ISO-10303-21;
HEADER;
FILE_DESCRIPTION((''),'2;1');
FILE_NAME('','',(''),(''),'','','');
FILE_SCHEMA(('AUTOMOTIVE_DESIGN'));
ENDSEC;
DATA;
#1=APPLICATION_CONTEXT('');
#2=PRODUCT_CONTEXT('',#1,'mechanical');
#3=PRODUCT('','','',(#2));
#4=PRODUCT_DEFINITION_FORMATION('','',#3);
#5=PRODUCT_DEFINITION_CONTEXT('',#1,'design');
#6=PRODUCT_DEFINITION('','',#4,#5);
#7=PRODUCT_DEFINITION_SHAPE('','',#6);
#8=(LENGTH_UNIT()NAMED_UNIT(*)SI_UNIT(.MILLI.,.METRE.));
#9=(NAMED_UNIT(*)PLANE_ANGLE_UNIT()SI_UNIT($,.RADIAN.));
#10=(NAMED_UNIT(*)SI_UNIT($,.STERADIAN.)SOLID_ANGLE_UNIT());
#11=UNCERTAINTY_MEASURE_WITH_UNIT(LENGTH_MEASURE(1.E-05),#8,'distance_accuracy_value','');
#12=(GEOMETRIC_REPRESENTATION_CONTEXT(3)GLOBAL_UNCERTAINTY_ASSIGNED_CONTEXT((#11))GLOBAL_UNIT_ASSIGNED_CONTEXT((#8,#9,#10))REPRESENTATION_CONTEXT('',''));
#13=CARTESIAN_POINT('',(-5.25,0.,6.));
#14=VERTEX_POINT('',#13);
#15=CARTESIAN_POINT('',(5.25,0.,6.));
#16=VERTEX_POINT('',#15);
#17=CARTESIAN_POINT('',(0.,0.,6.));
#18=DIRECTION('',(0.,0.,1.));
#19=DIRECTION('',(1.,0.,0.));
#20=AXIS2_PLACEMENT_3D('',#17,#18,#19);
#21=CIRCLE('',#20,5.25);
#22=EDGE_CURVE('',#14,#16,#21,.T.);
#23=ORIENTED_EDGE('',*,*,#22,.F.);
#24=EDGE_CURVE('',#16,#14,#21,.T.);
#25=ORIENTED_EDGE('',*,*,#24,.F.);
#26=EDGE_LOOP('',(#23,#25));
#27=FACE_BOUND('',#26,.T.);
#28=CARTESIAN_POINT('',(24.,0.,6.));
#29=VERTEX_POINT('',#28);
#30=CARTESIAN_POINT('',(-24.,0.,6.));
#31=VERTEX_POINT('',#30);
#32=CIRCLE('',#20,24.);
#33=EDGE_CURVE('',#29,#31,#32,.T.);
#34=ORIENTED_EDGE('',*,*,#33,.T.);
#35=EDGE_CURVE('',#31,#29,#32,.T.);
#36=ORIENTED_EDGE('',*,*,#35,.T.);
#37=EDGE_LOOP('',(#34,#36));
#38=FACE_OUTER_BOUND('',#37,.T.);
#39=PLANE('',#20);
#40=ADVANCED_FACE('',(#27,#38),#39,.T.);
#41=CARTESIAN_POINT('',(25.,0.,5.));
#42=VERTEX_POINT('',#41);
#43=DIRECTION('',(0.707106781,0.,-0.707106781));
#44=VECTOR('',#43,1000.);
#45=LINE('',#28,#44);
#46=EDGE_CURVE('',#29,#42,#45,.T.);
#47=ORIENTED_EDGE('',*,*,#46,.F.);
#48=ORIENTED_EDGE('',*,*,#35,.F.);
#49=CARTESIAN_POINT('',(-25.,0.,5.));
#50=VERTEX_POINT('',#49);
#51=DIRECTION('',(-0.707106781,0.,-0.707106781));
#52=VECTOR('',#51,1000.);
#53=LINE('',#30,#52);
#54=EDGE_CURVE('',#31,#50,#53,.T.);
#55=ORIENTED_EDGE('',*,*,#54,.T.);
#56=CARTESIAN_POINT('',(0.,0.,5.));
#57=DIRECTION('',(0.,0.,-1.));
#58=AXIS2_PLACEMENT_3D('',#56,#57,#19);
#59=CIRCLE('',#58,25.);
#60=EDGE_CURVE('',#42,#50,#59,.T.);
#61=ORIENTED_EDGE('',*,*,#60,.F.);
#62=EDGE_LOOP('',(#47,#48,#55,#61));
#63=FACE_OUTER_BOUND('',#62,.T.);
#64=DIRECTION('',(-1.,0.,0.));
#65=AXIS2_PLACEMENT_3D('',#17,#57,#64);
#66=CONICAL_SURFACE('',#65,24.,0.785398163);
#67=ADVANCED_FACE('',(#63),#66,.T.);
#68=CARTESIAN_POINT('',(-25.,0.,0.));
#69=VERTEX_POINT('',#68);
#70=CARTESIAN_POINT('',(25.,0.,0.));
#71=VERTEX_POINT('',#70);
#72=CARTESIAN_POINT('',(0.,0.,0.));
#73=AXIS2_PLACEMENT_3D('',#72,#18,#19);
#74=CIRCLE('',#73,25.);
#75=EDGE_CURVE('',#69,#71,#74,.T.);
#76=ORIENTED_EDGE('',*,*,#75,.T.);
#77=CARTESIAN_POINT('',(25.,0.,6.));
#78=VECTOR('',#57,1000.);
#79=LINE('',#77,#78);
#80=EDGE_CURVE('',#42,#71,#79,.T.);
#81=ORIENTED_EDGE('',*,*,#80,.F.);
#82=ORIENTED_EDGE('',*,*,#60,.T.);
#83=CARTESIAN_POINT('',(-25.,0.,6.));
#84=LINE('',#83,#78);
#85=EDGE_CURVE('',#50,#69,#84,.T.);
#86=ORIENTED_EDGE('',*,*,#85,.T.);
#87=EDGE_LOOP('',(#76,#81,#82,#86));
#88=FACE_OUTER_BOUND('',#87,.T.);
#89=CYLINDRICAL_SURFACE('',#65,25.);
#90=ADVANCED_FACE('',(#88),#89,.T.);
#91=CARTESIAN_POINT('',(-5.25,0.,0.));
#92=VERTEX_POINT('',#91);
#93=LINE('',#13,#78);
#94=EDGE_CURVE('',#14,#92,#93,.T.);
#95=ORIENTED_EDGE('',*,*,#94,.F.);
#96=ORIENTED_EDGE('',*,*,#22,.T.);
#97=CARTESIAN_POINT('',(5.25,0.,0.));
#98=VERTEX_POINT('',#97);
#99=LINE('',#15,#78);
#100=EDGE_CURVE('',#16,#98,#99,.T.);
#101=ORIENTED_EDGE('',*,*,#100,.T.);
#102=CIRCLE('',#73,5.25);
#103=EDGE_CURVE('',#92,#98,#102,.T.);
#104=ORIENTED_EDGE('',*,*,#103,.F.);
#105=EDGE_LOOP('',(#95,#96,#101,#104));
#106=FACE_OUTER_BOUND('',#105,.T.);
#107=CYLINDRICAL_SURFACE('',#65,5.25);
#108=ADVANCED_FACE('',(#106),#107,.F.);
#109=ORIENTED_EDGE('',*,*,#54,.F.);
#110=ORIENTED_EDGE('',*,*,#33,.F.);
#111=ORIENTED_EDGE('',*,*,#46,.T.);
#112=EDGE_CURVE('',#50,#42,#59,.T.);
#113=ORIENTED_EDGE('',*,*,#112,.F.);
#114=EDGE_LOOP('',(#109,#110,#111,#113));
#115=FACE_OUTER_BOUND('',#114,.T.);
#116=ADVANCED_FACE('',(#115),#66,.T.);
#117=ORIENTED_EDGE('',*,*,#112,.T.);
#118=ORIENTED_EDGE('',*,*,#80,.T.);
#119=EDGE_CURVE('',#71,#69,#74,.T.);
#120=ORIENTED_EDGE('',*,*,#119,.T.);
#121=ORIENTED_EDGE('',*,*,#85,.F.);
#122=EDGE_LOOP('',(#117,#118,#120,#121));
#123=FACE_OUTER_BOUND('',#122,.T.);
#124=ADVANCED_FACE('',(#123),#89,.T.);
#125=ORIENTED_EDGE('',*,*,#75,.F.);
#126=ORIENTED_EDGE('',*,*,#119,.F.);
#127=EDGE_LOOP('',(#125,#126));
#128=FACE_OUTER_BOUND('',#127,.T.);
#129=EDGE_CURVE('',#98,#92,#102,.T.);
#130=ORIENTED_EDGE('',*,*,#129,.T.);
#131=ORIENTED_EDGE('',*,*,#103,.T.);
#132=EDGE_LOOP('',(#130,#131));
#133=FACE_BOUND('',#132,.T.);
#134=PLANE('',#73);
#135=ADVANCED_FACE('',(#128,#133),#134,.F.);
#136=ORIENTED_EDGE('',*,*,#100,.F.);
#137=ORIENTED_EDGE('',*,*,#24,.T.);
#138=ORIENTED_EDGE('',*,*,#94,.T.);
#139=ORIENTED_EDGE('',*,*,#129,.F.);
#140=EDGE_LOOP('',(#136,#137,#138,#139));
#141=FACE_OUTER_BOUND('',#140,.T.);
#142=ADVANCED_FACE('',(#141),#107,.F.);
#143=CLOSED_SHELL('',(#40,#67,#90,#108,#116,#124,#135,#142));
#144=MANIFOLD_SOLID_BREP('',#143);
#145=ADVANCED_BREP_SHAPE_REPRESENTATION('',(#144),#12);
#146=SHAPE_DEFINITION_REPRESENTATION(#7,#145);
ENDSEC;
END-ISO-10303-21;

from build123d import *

# Parameters (mm, degrees)
SKETCH_1_R      = 25
SKETCH_1_R_2    = 5.25
EXTRUDE_1_DEPTH = 6
CHAMFER_1_SIZE  = 1


with BuildPart() as part:
    # 草图1 → 凸台-拉伸1 (new body)
    with BuildSketch(Plane.XY):
        Circle(SKETCH_1_R)
        Circle(SKETCH_1_R_2, mode=Mode.SUBTRACT)
    extrude(amount=EXTRUDE_1_DEPTH)

    # 倒角1
    chamfer_1_edges = [part.edges().sort_by_distance(p)[0] for p in [
        (-25, 0, 6),
    ]]
    chamfer(chamfer_1_edges, length=CHAMFER_1_SIZE)


solid = part.part
